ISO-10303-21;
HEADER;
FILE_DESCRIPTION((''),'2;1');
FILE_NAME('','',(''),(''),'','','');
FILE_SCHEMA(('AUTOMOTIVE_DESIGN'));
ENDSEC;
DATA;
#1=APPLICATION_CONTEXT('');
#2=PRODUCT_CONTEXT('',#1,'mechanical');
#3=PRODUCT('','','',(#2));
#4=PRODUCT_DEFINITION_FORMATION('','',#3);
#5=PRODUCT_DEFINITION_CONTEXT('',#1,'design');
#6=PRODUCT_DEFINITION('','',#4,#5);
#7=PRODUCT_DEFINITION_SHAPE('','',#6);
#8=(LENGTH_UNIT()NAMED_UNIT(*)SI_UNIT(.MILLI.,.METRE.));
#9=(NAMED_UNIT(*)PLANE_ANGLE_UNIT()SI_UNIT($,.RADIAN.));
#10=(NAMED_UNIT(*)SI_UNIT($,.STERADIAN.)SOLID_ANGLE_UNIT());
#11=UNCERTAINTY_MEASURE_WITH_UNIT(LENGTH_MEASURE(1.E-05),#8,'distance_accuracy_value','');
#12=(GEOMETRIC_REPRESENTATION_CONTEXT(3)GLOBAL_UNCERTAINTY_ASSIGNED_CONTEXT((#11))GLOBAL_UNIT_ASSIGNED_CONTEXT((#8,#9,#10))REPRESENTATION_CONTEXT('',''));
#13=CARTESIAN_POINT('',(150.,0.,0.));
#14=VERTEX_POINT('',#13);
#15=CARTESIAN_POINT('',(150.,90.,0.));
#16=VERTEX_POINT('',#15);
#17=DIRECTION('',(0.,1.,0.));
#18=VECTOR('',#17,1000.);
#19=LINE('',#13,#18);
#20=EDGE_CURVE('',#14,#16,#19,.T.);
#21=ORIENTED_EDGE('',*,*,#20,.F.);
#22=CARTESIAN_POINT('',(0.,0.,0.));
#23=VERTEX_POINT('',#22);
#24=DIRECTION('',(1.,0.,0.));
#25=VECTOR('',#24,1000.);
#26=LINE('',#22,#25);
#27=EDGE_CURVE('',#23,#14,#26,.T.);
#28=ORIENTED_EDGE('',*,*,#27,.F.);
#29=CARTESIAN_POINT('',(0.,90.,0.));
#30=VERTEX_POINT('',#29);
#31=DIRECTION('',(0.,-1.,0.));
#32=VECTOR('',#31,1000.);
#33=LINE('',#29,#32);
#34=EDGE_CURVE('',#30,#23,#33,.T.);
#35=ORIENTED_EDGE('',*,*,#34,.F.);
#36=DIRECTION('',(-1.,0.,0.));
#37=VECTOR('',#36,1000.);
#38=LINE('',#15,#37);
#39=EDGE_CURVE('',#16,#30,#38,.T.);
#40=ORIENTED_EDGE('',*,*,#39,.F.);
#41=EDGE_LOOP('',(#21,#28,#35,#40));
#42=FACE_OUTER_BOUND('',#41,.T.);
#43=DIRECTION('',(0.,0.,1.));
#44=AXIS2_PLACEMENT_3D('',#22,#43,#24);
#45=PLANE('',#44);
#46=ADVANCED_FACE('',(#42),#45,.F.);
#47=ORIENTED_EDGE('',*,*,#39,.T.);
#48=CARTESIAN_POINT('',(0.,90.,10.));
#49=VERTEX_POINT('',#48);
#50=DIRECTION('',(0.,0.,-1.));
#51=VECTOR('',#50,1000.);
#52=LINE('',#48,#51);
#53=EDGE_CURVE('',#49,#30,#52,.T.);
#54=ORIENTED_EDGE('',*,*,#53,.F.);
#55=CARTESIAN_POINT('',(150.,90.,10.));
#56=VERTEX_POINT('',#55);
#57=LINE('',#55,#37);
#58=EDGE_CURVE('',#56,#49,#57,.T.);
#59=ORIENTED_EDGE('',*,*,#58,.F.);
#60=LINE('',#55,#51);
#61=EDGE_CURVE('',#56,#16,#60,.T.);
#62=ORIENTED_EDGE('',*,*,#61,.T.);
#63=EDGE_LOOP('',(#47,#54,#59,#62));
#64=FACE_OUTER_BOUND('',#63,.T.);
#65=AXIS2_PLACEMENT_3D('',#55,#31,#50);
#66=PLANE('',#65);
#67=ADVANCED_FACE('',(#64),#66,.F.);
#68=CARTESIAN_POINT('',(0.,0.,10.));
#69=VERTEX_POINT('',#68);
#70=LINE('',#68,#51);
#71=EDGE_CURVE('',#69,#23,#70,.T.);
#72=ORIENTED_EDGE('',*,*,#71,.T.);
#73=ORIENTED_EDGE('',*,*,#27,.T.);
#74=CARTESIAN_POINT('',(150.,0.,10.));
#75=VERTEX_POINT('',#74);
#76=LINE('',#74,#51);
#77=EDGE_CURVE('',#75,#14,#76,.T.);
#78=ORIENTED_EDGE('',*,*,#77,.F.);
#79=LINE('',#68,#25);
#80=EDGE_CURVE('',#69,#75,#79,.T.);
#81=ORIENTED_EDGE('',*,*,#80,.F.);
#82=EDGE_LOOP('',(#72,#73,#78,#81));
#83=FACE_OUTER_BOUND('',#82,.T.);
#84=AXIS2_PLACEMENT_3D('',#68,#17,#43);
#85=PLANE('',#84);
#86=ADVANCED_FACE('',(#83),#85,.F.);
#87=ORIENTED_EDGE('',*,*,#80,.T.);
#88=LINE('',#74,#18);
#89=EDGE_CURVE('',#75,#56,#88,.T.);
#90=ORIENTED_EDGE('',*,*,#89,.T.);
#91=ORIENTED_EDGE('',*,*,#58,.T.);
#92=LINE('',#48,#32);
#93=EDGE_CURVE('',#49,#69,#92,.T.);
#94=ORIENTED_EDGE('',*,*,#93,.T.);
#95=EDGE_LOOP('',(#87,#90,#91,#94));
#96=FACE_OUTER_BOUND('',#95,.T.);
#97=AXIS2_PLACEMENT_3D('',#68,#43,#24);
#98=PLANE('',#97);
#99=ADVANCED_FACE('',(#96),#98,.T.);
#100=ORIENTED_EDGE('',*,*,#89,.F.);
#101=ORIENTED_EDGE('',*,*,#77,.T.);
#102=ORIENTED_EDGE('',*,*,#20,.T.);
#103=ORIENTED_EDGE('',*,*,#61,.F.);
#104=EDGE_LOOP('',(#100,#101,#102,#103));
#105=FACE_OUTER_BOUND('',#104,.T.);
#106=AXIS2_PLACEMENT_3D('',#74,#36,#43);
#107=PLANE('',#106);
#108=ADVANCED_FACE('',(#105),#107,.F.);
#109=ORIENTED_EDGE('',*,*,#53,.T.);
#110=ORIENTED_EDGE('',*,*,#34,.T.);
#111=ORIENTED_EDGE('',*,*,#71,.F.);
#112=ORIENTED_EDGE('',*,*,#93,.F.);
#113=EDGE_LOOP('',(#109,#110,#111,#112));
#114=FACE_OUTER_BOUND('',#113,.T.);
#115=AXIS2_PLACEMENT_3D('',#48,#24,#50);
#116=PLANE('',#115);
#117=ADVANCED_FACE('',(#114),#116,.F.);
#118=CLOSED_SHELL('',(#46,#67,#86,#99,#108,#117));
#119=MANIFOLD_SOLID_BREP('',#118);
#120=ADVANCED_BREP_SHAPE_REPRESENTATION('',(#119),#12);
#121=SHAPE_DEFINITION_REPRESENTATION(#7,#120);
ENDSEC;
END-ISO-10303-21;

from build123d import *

# Parameters (mm, degrees)
SKETCH_1_W      = 150
SKETCH_1_H      = 90
EXTRUDE_1_DEPTH = 10


with BuildPart() as part:
    # 草图1 → 凸台-拉伸1 (new body)
    with BuildSketch(Plane.XY):
        with Locations((75, 45)):
            Rectangle(SKETCH_1_W, SKETCH_1_H)
    extrude(amount=EXTRUDE_1_DEPTH)


solid = part.part
